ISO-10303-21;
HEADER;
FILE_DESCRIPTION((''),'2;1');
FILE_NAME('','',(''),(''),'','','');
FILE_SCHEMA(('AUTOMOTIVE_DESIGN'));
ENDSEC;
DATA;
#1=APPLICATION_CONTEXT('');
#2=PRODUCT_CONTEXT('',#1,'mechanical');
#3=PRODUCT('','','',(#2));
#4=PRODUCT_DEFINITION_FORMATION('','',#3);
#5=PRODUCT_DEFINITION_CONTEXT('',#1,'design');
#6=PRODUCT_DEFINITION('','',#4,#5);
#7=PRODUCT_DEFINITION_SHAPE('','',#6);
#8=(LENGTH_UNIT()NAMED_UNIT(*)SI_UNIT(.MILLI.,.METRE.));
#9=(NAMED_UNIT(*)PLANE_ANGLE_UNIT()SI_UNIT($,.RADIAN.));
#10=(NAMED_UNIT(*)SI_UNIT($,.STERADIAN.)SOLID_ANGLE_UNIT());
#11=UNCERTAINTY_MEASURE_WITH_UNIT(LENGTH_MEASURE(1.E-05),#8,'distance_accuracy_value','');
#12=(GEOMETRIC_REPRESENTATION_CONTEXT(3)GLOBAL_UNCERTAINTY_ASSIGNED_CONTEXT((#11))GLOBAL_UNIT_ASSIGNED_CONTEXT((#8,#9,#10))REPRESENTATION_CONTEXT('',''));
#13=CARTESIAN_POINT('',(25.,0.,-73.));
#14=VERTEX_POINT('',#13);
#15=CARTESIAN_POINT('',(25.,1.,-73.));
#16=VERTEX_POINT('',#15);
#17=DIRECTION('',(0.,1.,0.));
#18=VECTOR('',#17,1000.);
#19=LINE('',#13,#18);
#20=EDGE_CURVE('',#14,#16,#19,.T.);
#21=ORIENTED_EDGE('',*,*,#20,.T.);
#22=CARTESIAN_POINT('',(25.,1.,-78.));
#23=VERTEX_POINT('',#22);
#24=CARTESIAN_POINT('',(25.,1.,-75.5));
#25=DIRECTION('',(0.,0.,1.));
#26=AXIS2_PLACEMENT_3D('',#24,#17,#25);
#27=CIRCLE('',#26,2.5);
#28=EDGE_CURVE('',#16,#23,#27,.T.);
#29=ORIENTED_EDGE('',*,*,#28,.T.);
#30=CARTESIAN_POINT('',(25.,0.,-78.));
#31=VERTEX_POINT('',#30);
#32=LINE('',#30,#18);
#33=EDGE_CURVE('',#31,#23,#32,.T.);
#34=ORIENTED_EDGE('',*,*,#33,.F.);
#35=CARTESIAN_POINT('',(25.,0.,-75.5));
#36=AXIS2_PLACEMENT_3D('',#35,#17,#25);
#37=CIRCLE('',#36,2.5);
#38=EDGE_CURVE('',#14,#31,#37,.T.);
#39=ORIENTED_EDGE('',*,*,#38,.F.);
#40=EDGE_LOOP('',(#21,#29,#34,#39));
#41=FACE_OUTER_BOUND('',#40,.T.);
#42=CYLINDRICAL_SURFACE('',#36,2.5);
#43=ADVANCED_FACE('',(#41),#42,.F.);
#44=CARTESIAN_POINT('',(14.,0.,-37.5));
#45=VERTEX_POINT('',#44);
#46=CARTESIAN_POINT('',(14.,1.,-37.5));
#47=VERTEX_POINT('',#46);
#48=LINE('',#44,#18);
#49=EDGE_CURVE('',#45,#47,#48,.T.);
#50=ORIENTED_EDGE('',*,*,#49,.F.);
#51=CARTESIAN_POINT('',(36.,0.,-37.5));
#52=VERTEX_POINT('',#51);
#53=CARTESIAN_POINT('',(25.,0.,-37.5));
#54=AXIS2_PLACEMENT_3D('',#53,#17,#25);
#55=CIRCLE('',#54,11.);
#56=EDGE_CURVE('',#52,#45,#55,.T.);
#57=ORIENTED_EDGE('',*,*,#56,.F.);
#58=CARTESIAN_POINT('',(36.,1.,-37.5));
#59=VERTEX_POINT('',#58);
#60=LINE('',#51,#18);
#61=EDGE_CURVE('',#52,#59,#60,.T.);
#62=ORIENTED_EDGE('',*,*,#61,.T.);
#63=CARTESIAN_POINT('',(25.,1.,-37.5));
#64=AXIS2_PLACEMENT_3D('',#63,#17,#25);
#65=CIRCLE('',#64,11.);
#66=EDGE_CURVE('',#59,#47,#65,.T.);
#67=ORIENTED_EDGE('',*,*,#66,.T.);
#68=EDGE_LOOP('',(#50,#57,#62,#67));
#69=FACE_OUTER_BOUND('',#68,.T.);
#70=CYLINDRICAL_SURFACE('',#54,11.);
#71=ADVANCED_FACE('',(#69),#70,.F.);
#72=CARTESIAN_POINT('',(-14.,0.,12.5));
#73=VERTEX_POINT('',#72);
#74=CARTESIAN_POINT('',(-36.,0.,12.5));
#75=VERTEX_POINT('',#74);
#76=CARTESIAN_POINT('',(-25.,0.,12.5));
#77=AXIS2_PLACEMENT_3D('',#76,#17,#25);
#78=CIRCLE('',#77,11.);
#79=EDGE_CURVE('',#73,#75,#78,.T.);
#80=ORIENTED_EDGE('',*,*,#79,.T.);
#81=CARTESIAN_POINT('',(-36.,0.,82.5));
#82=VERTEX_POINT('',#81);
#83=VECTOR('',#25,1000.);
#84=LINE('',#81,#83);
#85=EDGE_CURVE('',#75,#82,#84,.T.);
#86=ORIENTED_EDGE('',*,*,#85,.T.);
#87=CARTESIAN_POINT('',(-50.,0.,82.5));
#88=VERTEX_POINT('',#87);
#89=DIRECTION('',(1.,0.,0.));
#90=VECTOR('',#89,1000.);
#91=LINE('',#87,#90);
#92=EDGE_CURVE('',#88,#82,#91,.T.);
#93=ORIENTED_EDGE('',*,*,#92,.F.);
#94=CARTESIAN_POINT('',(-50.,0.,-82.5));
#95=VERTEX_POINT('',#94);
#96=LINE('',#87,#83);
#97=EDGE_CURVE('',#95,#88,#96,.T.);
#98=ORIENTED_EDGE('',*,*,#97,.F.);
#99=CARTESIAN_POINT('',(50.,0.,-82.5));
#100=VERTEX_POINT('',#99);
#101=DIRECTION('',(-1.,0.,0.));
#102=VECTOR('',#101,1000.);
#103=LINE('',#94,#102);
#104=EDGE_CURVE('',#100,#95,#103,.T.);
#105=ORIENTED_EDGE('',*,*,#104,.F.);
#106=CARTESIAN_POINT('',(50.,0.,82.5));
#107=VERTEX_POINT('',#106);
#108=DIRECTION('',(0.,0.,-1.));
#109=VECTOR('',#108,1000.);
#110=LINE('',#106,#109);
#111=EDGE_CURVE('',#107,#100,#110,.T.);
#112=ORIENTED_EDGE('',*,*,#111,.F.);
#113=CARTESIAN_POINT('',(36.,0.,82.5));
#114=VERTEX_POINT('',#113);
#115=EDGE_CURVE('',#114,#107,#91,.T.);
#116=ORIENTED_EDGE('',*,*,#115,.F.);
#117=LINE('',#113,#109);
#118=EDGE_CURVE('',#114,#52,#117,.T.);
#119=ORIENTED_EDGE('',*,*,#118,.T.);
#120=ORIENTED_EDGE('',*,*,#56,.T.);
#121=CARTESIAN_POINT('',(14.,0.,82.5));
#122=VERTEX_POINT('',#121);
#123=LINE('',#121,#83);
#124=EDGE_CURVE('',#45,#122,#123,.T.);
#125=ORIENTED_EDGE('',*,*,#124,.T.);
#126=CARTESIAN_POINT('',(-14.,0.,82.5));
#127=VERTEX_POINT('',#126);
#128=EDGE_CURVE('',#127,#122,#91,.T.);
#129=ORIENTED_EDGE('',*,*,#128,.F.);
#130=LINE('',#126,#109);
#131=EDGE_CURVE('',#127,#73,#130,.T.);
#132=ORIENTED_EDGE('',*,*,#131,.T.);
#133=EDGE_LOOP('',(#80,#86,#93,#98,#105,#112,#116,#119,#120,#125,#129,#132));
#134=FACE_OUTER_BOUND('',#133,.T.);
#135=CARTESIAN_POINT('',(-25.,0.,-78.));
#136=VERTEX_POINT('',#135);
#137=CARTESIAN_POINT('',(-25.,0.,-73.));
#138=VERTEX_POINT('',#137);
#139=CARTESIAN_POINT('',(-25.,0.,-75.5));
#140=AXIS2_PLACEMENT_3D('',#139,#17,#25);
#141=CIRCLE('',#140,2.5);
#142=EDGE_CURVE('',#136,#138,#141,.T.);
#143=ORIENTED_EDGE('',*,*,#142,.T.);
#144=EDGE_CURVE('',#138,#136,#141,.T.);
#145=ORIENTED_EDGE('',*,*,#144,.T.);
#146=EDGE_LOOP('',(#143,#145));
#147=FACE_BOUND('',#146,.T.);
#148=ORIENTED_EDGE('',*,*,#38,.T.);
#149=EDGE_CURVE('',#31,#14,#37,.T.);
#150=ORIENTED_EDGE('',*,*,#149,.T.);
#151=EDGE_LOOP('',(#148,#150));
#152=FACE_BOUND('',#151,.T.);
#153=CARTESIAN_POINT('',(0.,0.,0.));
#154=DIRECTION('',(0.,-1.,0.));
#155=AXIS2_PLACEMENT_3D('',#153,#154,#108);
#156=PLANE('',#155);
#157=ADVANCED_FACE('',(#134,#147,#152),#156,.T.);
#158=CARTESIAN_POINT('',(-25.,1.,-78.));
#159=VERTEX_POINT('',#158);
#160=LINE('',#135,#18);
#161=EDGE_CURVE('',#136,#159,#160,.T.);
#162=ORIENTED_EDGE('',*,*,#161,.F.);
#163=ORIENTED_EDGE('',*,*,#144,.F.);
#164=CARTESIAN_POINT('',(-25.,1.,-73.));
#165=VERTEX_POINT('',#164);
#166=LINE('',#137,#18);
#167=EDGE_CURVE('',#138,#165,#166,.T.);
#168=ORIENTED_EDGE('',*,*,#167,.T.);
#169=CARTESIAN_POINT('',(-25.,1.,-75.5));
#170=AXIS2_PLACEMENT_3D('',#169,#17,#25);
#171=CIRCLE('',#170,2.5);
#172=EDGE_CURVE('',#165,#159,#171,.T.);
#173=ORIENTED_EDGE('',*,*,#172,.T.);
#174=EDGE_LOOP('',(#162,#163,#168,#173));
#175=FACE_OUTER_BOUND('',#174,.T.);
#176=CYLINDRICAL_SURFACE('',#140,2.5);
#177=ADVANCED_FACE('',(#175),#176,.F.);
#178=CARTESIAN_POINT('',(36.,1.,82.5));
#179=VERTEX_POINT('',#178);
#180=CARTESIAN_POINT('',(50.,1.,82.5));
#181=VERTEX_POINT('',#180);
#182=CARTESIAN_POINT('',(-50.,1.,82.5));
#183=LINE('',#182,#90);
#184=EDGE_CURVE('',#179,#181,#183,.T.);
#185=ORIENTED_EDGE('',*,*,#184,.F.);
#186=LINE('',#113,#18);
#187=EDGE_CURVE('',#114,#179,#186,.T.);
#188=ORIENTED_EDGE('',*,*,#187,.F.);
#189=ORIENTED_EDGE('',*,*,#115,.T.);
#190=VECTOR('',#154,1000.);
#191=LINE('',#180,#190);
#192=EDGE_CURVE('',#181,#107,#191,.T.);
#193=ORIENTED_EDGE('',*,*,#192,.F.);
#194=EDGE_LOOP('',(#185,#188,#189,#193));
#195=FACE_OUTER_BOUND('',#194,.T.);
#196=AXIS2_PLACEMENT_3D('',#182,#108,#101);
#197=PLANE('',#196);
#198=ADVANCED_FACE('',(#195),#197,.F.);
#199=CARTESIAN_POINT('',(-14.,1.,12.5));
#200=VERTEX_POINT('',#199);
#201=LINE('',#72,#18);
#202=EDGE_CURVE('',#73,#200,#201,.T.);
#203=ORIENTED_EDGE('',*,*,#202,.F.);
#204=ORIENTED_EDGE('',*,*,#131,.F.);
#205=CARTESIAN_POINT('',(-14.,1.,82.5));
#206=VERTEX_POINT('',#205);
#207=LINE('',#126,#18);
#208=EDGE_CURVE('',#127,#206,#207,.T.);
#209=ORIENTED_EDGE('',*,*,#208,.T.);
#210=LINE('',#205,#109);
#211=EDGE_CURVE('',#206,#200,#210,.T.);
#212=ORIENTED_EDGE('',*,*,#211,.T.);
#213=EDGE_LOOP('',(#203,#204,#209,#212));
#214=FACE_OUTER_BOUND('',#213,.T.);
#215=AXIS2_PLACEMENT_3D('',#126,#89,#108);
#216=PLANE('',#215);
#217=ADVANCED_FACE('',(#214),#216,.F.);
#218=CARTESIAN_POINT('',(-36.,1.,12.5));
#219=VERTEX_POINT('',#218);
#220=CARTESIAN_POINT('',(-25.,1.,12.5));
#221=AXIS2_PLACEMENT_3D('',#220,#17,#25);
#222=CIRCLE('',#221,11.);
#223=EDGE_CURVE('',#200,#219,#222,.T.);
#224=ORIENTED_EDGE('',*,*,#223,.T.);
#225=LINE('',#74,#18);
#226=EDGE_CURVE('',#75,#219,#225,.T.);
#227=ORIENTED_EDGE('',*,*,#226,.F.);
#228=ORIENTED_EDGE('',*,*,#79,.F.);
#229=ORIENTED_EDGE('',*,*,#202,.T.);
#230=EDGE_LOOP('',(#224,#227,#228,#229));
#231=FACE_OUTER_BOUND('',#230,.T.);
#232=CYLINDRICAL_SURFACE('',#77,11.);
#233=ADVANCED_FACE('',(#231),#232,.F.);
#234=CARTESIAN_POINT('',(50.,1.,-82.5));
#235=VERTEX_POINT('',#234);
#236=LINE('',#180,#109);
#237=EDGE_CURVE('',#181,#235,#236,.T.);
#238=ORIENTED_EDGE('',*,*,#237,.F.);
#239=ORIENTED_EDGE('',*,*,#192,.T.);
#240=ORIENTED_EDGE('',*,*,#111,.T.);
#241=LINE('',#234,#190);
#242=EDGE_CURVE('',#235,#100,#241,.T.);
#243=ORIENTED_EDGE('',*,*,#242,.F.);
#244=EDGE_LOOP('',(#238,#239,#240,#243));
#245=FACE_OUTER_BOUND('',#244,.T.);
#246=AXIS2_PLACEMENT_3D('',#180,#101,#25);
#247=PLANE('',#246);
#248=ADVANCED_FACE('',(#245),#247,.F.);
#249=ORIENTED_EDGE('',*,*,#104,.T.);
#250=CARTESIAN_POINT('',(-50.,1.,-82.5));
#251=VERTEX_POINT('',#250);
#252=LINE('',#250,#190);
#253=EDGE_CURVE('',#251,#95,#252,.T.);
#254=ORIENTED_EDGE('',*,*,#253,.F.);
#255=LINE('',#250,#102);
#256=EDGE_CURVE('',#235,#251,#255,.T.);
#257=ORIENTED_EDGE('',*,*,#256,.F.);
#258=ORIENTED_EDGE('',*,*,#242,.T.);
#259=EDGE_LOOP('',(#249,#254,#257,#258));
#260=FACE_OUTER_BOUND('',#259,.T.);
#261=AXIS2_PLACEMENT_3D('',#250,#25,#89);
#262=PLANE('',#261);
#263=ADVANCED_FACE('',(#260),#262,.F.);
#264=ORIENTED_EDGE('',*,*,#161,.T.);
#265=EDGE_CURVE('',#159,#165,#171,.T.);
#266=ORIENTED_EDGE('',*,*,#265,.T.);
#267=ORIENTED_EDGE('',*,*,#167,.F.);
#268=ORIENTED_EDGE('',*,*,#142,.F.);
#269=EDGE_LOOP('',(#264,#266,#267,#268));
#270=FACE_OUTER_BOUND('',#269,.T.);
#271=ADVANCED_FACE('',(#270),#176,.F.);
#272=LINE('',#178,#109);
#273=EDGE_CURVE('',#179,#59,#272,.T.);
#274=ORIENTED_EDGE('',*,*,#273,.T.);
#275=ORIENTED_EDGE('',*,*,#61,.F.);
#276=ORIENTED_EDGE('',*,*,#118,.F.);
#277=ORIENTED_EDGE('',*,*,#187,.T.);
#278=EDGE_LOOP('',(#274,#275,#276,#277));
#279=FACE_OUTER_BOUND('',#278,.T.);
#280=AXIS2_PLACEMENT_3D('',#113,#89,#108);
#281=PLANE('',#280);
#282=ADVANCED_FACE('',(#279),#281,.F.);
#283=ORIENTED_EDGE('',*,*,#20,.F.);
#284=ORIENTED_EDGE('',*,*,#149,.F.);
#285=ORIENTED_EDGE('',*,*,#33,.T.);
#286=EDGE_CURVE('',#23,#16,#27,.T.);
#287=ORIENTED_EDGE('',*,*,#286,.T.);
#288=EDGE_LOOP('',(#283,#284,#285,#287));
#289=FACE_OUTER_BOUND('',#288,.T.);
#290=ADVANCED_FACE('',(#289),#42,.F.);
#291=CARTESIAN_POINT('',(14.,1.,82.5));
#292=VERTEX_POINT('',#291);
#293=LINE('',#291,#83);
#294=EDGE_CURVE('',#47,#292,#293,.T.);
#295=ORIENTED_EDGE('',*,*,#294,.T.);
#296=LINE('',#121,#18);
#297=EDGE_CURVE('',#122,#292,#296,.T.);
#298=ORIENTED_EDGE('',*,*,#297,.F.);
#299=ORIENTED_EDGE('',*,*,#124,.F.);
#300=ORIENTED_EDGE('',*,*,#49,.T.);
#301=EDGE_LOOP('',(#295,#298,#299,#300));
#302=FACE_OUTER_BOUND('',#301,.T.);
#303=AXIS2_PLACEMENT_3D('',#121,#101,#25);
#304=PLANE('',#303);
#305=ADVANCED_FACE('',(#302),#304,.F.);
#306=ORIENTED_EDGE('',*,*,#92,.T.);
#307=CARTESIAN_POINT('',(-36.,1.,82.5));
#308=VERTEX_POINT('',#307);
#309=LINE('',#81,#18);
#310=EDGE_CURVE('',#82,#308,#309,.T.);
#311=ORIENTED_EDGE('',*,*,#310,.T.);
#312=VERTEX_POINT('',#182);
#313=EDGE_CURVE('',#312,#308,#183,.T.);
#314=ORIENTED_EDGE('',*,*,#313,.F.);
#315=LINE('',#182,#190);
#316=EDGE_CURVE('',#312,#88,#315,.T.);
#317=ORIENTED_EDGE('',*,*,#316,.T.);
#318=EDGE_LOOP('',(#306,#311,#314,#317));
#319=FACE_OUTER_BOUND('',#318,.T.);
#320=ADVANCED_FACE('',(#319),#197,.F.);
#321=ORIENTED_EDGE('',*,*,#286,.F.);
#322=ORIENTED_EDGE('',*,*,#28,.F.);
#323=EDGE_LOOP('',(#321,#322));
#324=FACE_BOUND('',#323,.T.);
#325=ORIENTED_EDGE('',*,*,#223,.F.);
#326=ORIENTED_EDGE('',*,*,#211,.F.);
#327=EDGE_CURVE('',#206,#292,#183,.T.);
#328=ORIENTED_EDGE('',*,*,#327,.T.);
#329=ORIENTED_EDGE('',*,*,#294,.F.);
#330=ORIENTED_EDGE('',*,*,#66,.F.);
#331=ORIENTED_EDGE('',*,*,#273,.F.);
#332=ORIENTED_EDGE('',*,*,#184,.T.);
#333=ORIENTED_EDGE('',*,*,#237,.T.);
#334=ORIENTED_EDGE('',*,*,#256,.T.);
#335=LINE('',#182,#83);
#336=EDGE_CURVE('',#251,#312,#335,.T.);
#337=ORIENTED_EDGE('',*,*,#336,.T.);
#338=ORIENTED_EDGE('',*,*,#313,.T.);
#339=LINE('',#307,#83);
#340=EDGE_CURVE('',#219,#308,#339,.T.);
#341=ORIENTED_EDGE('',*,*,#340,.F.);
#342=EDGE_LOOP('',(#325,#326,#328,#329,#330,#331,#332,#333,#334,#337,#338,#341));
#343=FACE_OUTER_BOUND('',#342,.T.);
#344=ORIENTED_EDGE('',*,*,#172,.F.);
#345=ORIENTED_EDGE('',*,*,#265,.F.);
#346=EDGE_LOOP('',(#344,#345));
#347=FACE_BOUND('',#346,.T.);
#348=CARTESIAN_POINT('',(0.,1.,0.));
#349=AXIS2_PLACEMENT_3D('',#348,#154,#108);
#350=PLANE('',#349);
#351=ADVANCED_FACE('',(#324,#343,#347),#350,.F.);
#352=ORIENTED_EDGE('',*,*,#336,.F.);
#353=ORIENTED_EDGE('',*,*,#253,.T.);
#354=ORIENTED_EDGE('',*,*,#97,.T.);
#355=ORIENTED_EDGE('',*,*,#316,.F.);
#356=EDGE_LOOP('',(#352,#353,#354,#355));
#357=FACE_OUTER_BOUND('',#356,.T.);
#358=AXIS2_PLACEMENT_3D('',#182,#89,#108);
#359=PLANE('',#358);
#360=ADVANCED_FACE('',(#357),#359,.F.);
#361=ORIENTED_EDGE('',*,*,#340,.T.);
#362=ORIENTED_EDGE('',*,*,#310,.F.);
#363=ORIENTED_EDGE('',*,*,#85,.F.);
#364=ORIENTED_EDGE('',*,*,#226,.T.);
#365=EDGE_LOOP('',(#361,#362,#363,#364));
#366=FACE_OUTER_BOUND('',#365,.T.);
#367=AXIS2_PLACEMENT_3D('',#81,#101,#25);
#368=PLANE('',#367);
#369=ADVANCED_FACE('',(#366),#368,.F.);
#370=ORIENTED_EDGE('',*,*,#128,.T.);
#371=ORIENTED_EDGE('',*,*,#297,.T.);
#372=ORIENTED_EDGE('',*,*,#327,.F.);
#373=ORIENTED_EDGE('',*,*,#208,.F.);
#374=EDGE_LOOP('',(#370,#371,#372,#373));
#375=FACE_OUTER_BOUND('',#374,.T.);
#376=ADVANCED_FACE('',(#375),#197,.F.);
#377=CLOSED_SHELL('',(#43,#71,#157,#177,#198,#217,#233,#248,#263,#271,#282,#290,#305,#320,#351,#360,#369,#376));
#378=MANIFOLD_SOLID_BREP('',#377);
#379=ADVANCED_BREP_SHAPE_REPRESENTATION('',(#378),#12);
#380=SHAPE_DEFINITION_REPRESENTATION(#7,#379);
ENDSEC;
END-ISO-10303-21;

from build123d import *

# Parameters (mm, degrees)
SKETCH_1_W          = 100
SKETCH_1_H          = 165
EXTRUDE_1_DEPTH     = 1
SKETCH_2_R          = 2.5
CUT_EXTRUDE_1_DEPTH = 97.474089786


with BuildPart() as part:
    # 草图1 → 凸台-拉伸1 (new body)
    with BuildSketch(Plane(origin=(0, 0, 0), x_dir=(1, 0, 0), z_dir=(0, 1, 0))):
        Rectangle(SKETCH_1_W, SKETCH_1_H)
    extrude(amount=EXTRUDE_1_DEPTH)

    # 草图2 → 切除-拉伸1 (cut, through all)
    with BuildSketch(Plane(origin=(0, 1, 0), x_dir=(1, 0, 0), z_dir=(0, 1, 0))):
        with Locations(Location((-25, 75.5, 0), (0, 0, 270))):
            Circle(SKETCH_2_R)
        with Locations(Location((25, 75.5, 0), (0, 0, 270))):
            Circle(SKETCH_2_R)
        with BuildLine():
            Line((-36, -82.5), (-36, -12.5))
            ThreePointArc((-36, -12.5), (-25, -1.5), (-14, -12.5))
            Line((-14, -12.5), (-14, -82.5))
            ThreePointArc((-14, -82.5), (-25, -93.5), (-36, -82.5))
        make_face()
        with BuildLine():
            Line((14, -82.5), (14, 37.5))
            ThreePointArc((14, 37.5), (25, 48.5), (36, 37.5))
            Line((36, 37.5), (36, -82.5))
            ThreePointArc((36, -82.5), (25, -93.5), (14, -82.5))
        make_face()
    extrude(amount=-CUT_EXTRUDE_1_DEPTH, mode=Mode.SUBTRACT)


solid = part.part
